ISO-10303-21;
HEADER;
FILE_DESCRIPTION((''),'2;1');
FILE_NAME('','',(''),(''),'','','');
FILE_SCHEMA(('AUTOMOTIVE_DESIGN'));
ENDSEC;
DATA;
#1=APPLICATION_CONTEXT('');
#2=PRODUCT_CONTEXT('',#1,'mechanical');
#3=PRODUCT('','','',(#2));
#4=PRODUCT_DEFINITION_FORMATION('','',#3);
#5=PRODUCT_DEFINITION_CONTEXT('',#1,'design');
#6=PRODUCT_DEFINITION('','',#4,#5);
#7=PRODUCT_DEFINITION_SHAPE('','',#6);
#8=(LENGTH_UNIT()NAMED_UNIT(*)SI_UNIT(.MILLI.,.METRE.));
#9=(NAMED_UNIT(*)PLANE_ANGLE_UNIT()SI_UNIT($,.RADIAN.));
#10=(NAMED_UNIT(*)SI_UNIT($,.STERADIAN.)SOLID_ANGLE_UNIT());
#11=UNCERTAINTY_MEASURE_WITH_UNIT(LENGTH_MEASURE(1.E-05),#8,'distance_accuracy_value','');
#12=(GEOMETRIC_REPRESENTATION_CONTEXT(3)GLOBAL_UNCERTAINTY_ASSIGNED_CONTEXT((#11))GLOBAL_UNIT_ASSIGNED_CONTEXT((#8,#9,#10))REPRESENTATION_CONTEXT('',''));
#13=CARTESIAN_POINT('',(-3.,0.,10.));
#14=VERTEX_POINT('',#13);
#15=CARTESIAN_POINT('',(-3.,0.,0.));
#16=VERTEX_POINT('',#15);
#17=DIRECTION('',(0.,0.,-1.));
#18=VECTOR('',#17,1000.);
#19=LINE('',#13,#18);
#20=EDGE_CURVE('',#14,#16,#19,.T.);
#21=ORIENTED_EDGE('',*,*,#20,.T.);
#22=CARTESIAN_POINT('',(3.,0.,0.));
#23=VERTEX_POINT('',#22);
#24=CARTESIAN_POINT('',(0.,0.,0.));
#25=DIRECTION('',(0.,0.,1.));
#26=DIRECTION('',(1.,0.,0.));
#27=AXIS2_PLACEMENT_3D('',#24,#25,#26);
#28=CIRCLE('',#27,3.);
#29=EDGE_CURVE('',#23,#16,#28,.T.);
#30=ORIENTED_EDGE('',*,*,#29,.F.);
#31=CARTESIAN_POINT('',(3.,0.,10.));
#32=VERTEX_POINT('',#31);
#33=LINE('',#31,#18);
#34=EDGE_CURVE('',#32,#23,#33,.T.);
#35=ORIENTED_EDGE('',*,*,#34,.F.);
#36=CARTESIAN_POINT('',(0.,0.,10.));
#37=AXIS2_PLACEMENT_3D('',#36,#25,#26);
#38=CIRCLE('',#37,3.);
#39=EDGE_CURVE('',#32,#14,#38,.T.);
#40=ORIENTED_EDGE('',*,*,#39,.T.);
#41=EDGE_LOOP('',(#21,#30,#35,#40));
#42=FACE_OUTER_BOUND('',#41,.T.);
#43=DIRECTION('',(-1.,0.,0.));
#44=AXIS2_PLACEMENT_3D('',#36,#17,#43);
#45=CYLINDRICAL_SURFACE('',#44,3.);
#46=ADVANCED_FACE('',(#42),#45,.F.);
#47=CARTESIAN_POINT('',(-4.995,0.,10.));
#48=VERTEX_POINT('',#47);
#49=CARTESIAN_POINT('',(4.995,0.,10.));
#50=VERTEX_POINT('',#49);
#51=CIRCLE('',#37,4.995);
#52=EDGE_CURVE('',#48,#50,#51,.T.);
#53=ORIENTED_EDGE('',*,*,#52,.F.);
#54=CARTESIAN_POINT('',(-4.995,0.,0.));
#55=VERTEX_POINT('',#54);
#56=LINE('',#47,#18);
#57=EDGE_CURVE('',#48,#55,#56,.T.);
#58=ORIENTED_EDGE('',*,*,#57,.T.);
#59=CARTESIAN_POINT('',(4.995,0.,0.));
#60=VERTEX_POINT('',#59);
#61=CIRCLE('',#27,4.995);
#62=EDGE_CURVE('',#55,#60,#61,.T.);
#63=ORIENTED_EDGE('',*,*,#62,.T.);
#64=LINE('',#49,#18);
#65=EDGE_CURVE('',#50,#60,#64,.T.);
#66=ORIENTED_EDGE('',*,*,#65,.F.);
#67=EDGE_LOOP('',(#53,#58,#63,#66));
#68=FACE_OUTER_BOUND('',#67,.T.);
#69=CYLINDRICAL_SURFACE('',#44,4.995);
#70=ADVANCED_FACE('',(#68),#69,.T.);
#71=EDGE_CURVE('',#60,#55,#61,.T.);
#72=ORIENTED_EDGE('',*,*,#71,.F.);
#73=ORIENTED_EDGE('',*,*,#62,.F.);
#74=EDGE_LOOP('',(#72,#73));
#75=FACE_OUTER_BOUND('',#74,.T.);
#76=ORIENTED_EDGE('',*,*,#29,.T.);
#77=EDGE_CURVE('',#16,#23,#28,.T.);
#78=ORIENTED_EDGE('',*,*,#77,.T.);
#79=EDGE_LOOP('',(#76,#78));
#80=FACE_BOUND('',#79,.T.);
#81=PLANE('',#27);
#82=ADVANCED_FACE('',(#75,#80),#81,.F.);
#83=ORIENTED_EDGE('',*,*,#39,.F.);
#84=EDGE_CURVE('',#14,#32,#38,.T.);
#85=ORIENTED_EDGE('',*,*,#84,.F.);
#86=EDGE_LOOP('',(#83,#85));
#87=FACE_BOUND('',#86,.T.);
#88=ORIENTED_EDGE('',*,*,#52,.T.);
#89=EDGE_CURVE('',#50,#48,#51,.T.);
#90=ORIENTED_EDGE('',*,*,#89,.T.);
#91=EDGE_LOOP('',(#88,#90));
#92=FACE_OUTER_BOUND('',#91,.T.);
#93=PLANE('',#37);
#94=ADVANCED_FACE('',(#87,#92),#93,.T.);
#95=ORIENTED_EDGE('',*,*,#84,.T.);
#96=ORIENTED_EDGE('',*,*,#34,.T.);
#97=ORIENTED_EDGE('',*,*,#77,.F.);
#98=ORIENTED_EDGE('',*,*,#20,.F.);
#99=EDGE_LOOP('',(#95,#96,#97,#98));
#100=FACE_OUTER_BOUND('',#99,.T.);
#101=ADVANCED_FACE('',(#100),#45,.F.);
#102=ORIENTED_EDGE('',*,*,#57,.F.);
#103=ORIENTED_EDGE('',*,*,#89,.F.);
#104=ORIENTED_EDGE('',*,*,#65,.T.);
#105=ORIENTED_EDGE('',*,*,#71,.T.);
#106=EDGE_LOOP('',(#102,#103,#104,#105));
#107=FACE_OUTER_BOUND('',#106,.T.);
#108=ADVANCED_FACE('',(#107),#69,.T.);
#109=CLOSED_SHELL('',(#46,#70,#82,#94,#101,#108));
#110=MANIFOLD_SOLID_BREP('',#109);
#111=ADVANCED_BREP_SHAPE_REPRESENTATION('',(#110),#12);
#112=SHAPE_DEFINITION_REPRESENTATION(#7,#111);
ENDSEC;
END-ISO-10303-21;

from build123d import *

# Parameters (mm, degrees)
SKETCH1_R           = 4.995
SKETCH1_R_2         = 3
BOSS_EXTRUDE1_DEPTH = 10


with BuildPart() as part:
    # Sketch1 → Boss-Extrude1 (new body)
    with BuildSketch(Plane.XY):
        Circle(SKETCH1_R)
        Circle(SKETCH1_R_2, mode=Mode.SUBTRACT)
    extrude(amount=BOSS_EXTRUDE1_DEPTH)


solid = part.part
